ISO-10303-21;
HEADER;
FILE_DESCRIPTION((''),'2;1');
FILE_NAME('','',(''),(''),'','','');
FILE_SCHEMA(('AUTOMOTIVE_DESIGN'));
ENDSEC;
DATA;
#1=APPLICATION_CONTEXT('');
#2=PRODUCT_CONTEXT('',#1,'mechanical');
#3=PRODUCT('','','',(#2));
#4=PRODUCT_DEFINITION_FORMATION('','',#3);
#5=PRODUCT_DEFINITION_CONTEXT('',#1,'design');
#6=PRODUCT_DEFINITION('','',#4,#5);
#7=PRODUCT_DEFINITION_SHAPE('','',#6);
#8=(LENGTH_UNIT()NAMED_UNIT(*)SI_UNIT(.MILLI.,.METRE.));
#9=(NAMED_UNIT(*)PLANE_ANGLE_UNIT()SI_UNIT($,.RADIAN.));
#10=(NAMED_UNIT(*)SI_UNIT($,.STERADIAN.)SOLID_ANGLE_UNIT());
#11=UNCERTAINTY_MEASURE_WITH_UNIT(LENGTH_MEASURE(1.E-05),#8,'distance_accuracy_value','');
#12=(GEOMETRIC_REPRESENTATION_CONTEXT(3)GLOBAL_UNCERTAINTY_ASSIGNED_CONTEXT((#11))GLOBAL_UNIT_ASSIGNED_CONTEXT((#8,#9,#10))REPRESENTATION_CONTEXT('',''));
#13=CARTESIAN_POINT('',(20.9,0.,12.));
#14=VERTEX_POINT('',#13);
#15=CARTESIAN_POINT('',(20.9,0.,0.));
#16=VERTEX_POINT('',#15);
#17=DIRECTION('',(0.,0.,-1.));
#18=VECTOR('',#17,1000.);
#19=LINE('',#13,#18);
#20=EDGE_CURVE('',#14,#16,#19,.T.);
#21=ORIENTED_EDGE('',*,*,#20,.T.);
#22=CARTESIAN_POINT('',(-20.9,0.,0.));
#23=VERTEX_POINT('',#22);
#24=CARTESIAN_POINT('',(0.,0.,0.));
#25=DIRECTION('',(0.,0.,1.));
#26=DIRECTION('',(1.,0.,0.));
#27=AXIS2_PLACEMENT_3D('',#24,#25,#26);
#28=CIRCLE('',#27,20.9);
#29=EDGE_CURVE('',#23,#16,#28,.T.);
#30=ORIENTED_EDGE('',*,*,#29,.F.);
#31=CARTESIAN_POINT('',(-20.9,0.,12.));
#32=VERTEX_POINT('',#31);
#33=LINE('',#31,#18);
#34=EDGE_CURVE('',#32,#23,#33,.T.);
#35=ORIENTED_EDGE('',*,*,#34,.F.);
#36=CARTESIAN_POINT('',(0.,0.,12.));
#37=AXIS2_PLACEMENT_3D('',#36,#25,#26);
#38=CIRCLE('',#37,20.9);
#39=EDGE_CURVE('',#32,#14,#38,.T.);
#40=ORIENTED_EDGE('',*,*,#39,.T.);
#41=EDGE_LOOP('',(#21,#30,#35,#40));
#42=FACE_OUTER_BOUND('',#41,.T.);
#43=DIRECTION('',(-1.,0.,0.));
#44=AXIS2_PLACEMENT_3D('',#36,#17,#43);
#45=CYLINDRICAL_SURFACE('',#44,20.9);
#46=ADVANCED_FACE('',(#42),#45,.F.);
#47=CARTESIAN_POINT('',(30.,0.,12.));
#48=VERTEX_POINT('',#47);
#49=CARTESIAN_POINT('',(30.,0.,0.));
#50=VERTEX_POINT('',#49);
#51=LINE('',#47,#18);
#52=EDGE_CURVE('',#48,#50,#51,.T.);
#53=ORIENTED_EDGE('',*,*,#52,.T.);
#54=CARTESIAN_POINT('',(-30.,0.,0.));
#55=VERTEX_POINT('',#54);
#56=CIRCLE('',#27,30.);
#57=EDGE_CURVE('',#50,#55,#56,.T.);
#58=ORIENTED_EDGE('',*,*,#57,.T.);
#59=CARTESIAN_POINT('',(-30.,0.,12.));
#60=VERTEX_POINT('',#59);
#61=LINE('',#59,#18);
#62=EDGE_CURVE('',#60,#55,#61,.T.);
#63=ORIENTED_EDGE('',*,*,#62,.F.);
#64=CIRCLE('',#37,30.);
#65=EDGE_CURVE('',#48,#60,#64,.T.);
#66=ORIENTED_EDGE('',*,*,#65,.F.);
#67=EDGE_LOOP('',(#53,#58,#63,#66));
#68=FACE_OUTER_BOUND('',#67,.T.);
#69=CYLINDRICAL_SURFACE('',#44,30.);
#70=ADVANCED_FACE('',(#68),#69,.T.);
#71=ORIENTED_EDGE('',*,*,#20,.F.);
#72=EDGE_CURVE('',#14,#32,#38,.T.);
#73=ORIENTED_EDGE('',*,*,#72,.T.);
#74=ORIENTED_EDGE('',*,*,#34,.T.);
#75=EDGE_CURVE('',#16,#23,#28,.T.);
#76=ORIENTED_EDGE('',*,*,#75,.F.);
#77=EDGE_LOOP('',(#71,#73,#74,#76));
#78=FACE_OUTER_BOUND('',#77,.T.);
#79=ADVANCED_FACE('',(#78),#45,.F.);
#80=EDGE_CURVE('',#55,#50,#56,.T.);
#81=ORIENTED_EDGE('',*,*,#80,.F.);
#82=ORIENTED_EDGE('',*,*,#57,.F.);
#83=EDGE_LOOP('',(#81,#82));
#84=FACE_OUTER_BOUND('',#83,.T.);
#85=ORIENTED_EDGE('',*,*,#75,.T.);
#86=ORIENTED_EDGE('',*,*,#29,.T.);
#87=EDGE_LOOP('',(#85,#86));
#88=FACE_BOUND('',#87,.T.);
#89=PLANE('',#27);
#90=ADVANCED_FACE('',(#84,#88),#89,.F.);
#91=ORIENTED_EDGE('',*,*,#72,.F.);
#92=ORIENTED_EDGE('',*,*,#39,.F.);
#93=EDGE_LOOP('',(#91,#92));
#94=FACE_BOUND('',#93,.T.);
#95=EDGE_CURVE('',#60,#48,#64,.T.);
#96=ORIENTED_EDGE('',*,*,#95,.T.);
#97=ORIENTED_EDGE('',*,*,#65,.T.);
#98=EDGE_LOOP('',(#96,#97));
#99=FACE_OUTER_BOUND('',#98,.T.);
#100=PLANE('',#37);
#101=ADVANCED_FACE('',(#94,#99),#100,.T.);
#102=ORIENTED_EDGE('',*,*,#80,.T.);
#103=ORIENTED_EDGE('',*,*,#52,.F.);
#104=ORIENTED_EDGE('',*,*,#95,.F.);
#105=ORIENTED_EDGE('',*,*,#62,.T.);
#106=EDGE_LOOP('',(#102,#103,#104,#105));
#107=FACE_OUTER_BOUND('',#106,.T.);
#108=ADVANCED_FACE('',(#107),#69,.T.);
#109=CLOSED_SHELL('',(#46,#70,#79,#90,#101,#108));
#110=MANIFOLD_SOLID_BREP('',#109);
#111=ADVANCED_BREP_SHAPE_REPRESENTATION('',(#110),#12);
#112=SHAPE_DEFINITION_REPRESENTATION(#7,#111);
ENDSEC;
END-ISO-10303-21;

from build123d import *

# Parameters (mm, degrees)
SKETCH1_R           = 30
SKETCH1_R_2         = 20.9
BOSS_EXTRUDE1_DEPTH = 12


with BuildPart() as part:
    # Sketch1 → Boss-Extrude1 (new body)
    with BuildSketch(Plane.XY):
        Circle(SKETCH1_R)
        Circle(SKETCH1_R_2, mode=Mode.SUBTRACT)
    extrude(amount=BOSS_EXTRUDE1_DEPTH)


solid = part.part
